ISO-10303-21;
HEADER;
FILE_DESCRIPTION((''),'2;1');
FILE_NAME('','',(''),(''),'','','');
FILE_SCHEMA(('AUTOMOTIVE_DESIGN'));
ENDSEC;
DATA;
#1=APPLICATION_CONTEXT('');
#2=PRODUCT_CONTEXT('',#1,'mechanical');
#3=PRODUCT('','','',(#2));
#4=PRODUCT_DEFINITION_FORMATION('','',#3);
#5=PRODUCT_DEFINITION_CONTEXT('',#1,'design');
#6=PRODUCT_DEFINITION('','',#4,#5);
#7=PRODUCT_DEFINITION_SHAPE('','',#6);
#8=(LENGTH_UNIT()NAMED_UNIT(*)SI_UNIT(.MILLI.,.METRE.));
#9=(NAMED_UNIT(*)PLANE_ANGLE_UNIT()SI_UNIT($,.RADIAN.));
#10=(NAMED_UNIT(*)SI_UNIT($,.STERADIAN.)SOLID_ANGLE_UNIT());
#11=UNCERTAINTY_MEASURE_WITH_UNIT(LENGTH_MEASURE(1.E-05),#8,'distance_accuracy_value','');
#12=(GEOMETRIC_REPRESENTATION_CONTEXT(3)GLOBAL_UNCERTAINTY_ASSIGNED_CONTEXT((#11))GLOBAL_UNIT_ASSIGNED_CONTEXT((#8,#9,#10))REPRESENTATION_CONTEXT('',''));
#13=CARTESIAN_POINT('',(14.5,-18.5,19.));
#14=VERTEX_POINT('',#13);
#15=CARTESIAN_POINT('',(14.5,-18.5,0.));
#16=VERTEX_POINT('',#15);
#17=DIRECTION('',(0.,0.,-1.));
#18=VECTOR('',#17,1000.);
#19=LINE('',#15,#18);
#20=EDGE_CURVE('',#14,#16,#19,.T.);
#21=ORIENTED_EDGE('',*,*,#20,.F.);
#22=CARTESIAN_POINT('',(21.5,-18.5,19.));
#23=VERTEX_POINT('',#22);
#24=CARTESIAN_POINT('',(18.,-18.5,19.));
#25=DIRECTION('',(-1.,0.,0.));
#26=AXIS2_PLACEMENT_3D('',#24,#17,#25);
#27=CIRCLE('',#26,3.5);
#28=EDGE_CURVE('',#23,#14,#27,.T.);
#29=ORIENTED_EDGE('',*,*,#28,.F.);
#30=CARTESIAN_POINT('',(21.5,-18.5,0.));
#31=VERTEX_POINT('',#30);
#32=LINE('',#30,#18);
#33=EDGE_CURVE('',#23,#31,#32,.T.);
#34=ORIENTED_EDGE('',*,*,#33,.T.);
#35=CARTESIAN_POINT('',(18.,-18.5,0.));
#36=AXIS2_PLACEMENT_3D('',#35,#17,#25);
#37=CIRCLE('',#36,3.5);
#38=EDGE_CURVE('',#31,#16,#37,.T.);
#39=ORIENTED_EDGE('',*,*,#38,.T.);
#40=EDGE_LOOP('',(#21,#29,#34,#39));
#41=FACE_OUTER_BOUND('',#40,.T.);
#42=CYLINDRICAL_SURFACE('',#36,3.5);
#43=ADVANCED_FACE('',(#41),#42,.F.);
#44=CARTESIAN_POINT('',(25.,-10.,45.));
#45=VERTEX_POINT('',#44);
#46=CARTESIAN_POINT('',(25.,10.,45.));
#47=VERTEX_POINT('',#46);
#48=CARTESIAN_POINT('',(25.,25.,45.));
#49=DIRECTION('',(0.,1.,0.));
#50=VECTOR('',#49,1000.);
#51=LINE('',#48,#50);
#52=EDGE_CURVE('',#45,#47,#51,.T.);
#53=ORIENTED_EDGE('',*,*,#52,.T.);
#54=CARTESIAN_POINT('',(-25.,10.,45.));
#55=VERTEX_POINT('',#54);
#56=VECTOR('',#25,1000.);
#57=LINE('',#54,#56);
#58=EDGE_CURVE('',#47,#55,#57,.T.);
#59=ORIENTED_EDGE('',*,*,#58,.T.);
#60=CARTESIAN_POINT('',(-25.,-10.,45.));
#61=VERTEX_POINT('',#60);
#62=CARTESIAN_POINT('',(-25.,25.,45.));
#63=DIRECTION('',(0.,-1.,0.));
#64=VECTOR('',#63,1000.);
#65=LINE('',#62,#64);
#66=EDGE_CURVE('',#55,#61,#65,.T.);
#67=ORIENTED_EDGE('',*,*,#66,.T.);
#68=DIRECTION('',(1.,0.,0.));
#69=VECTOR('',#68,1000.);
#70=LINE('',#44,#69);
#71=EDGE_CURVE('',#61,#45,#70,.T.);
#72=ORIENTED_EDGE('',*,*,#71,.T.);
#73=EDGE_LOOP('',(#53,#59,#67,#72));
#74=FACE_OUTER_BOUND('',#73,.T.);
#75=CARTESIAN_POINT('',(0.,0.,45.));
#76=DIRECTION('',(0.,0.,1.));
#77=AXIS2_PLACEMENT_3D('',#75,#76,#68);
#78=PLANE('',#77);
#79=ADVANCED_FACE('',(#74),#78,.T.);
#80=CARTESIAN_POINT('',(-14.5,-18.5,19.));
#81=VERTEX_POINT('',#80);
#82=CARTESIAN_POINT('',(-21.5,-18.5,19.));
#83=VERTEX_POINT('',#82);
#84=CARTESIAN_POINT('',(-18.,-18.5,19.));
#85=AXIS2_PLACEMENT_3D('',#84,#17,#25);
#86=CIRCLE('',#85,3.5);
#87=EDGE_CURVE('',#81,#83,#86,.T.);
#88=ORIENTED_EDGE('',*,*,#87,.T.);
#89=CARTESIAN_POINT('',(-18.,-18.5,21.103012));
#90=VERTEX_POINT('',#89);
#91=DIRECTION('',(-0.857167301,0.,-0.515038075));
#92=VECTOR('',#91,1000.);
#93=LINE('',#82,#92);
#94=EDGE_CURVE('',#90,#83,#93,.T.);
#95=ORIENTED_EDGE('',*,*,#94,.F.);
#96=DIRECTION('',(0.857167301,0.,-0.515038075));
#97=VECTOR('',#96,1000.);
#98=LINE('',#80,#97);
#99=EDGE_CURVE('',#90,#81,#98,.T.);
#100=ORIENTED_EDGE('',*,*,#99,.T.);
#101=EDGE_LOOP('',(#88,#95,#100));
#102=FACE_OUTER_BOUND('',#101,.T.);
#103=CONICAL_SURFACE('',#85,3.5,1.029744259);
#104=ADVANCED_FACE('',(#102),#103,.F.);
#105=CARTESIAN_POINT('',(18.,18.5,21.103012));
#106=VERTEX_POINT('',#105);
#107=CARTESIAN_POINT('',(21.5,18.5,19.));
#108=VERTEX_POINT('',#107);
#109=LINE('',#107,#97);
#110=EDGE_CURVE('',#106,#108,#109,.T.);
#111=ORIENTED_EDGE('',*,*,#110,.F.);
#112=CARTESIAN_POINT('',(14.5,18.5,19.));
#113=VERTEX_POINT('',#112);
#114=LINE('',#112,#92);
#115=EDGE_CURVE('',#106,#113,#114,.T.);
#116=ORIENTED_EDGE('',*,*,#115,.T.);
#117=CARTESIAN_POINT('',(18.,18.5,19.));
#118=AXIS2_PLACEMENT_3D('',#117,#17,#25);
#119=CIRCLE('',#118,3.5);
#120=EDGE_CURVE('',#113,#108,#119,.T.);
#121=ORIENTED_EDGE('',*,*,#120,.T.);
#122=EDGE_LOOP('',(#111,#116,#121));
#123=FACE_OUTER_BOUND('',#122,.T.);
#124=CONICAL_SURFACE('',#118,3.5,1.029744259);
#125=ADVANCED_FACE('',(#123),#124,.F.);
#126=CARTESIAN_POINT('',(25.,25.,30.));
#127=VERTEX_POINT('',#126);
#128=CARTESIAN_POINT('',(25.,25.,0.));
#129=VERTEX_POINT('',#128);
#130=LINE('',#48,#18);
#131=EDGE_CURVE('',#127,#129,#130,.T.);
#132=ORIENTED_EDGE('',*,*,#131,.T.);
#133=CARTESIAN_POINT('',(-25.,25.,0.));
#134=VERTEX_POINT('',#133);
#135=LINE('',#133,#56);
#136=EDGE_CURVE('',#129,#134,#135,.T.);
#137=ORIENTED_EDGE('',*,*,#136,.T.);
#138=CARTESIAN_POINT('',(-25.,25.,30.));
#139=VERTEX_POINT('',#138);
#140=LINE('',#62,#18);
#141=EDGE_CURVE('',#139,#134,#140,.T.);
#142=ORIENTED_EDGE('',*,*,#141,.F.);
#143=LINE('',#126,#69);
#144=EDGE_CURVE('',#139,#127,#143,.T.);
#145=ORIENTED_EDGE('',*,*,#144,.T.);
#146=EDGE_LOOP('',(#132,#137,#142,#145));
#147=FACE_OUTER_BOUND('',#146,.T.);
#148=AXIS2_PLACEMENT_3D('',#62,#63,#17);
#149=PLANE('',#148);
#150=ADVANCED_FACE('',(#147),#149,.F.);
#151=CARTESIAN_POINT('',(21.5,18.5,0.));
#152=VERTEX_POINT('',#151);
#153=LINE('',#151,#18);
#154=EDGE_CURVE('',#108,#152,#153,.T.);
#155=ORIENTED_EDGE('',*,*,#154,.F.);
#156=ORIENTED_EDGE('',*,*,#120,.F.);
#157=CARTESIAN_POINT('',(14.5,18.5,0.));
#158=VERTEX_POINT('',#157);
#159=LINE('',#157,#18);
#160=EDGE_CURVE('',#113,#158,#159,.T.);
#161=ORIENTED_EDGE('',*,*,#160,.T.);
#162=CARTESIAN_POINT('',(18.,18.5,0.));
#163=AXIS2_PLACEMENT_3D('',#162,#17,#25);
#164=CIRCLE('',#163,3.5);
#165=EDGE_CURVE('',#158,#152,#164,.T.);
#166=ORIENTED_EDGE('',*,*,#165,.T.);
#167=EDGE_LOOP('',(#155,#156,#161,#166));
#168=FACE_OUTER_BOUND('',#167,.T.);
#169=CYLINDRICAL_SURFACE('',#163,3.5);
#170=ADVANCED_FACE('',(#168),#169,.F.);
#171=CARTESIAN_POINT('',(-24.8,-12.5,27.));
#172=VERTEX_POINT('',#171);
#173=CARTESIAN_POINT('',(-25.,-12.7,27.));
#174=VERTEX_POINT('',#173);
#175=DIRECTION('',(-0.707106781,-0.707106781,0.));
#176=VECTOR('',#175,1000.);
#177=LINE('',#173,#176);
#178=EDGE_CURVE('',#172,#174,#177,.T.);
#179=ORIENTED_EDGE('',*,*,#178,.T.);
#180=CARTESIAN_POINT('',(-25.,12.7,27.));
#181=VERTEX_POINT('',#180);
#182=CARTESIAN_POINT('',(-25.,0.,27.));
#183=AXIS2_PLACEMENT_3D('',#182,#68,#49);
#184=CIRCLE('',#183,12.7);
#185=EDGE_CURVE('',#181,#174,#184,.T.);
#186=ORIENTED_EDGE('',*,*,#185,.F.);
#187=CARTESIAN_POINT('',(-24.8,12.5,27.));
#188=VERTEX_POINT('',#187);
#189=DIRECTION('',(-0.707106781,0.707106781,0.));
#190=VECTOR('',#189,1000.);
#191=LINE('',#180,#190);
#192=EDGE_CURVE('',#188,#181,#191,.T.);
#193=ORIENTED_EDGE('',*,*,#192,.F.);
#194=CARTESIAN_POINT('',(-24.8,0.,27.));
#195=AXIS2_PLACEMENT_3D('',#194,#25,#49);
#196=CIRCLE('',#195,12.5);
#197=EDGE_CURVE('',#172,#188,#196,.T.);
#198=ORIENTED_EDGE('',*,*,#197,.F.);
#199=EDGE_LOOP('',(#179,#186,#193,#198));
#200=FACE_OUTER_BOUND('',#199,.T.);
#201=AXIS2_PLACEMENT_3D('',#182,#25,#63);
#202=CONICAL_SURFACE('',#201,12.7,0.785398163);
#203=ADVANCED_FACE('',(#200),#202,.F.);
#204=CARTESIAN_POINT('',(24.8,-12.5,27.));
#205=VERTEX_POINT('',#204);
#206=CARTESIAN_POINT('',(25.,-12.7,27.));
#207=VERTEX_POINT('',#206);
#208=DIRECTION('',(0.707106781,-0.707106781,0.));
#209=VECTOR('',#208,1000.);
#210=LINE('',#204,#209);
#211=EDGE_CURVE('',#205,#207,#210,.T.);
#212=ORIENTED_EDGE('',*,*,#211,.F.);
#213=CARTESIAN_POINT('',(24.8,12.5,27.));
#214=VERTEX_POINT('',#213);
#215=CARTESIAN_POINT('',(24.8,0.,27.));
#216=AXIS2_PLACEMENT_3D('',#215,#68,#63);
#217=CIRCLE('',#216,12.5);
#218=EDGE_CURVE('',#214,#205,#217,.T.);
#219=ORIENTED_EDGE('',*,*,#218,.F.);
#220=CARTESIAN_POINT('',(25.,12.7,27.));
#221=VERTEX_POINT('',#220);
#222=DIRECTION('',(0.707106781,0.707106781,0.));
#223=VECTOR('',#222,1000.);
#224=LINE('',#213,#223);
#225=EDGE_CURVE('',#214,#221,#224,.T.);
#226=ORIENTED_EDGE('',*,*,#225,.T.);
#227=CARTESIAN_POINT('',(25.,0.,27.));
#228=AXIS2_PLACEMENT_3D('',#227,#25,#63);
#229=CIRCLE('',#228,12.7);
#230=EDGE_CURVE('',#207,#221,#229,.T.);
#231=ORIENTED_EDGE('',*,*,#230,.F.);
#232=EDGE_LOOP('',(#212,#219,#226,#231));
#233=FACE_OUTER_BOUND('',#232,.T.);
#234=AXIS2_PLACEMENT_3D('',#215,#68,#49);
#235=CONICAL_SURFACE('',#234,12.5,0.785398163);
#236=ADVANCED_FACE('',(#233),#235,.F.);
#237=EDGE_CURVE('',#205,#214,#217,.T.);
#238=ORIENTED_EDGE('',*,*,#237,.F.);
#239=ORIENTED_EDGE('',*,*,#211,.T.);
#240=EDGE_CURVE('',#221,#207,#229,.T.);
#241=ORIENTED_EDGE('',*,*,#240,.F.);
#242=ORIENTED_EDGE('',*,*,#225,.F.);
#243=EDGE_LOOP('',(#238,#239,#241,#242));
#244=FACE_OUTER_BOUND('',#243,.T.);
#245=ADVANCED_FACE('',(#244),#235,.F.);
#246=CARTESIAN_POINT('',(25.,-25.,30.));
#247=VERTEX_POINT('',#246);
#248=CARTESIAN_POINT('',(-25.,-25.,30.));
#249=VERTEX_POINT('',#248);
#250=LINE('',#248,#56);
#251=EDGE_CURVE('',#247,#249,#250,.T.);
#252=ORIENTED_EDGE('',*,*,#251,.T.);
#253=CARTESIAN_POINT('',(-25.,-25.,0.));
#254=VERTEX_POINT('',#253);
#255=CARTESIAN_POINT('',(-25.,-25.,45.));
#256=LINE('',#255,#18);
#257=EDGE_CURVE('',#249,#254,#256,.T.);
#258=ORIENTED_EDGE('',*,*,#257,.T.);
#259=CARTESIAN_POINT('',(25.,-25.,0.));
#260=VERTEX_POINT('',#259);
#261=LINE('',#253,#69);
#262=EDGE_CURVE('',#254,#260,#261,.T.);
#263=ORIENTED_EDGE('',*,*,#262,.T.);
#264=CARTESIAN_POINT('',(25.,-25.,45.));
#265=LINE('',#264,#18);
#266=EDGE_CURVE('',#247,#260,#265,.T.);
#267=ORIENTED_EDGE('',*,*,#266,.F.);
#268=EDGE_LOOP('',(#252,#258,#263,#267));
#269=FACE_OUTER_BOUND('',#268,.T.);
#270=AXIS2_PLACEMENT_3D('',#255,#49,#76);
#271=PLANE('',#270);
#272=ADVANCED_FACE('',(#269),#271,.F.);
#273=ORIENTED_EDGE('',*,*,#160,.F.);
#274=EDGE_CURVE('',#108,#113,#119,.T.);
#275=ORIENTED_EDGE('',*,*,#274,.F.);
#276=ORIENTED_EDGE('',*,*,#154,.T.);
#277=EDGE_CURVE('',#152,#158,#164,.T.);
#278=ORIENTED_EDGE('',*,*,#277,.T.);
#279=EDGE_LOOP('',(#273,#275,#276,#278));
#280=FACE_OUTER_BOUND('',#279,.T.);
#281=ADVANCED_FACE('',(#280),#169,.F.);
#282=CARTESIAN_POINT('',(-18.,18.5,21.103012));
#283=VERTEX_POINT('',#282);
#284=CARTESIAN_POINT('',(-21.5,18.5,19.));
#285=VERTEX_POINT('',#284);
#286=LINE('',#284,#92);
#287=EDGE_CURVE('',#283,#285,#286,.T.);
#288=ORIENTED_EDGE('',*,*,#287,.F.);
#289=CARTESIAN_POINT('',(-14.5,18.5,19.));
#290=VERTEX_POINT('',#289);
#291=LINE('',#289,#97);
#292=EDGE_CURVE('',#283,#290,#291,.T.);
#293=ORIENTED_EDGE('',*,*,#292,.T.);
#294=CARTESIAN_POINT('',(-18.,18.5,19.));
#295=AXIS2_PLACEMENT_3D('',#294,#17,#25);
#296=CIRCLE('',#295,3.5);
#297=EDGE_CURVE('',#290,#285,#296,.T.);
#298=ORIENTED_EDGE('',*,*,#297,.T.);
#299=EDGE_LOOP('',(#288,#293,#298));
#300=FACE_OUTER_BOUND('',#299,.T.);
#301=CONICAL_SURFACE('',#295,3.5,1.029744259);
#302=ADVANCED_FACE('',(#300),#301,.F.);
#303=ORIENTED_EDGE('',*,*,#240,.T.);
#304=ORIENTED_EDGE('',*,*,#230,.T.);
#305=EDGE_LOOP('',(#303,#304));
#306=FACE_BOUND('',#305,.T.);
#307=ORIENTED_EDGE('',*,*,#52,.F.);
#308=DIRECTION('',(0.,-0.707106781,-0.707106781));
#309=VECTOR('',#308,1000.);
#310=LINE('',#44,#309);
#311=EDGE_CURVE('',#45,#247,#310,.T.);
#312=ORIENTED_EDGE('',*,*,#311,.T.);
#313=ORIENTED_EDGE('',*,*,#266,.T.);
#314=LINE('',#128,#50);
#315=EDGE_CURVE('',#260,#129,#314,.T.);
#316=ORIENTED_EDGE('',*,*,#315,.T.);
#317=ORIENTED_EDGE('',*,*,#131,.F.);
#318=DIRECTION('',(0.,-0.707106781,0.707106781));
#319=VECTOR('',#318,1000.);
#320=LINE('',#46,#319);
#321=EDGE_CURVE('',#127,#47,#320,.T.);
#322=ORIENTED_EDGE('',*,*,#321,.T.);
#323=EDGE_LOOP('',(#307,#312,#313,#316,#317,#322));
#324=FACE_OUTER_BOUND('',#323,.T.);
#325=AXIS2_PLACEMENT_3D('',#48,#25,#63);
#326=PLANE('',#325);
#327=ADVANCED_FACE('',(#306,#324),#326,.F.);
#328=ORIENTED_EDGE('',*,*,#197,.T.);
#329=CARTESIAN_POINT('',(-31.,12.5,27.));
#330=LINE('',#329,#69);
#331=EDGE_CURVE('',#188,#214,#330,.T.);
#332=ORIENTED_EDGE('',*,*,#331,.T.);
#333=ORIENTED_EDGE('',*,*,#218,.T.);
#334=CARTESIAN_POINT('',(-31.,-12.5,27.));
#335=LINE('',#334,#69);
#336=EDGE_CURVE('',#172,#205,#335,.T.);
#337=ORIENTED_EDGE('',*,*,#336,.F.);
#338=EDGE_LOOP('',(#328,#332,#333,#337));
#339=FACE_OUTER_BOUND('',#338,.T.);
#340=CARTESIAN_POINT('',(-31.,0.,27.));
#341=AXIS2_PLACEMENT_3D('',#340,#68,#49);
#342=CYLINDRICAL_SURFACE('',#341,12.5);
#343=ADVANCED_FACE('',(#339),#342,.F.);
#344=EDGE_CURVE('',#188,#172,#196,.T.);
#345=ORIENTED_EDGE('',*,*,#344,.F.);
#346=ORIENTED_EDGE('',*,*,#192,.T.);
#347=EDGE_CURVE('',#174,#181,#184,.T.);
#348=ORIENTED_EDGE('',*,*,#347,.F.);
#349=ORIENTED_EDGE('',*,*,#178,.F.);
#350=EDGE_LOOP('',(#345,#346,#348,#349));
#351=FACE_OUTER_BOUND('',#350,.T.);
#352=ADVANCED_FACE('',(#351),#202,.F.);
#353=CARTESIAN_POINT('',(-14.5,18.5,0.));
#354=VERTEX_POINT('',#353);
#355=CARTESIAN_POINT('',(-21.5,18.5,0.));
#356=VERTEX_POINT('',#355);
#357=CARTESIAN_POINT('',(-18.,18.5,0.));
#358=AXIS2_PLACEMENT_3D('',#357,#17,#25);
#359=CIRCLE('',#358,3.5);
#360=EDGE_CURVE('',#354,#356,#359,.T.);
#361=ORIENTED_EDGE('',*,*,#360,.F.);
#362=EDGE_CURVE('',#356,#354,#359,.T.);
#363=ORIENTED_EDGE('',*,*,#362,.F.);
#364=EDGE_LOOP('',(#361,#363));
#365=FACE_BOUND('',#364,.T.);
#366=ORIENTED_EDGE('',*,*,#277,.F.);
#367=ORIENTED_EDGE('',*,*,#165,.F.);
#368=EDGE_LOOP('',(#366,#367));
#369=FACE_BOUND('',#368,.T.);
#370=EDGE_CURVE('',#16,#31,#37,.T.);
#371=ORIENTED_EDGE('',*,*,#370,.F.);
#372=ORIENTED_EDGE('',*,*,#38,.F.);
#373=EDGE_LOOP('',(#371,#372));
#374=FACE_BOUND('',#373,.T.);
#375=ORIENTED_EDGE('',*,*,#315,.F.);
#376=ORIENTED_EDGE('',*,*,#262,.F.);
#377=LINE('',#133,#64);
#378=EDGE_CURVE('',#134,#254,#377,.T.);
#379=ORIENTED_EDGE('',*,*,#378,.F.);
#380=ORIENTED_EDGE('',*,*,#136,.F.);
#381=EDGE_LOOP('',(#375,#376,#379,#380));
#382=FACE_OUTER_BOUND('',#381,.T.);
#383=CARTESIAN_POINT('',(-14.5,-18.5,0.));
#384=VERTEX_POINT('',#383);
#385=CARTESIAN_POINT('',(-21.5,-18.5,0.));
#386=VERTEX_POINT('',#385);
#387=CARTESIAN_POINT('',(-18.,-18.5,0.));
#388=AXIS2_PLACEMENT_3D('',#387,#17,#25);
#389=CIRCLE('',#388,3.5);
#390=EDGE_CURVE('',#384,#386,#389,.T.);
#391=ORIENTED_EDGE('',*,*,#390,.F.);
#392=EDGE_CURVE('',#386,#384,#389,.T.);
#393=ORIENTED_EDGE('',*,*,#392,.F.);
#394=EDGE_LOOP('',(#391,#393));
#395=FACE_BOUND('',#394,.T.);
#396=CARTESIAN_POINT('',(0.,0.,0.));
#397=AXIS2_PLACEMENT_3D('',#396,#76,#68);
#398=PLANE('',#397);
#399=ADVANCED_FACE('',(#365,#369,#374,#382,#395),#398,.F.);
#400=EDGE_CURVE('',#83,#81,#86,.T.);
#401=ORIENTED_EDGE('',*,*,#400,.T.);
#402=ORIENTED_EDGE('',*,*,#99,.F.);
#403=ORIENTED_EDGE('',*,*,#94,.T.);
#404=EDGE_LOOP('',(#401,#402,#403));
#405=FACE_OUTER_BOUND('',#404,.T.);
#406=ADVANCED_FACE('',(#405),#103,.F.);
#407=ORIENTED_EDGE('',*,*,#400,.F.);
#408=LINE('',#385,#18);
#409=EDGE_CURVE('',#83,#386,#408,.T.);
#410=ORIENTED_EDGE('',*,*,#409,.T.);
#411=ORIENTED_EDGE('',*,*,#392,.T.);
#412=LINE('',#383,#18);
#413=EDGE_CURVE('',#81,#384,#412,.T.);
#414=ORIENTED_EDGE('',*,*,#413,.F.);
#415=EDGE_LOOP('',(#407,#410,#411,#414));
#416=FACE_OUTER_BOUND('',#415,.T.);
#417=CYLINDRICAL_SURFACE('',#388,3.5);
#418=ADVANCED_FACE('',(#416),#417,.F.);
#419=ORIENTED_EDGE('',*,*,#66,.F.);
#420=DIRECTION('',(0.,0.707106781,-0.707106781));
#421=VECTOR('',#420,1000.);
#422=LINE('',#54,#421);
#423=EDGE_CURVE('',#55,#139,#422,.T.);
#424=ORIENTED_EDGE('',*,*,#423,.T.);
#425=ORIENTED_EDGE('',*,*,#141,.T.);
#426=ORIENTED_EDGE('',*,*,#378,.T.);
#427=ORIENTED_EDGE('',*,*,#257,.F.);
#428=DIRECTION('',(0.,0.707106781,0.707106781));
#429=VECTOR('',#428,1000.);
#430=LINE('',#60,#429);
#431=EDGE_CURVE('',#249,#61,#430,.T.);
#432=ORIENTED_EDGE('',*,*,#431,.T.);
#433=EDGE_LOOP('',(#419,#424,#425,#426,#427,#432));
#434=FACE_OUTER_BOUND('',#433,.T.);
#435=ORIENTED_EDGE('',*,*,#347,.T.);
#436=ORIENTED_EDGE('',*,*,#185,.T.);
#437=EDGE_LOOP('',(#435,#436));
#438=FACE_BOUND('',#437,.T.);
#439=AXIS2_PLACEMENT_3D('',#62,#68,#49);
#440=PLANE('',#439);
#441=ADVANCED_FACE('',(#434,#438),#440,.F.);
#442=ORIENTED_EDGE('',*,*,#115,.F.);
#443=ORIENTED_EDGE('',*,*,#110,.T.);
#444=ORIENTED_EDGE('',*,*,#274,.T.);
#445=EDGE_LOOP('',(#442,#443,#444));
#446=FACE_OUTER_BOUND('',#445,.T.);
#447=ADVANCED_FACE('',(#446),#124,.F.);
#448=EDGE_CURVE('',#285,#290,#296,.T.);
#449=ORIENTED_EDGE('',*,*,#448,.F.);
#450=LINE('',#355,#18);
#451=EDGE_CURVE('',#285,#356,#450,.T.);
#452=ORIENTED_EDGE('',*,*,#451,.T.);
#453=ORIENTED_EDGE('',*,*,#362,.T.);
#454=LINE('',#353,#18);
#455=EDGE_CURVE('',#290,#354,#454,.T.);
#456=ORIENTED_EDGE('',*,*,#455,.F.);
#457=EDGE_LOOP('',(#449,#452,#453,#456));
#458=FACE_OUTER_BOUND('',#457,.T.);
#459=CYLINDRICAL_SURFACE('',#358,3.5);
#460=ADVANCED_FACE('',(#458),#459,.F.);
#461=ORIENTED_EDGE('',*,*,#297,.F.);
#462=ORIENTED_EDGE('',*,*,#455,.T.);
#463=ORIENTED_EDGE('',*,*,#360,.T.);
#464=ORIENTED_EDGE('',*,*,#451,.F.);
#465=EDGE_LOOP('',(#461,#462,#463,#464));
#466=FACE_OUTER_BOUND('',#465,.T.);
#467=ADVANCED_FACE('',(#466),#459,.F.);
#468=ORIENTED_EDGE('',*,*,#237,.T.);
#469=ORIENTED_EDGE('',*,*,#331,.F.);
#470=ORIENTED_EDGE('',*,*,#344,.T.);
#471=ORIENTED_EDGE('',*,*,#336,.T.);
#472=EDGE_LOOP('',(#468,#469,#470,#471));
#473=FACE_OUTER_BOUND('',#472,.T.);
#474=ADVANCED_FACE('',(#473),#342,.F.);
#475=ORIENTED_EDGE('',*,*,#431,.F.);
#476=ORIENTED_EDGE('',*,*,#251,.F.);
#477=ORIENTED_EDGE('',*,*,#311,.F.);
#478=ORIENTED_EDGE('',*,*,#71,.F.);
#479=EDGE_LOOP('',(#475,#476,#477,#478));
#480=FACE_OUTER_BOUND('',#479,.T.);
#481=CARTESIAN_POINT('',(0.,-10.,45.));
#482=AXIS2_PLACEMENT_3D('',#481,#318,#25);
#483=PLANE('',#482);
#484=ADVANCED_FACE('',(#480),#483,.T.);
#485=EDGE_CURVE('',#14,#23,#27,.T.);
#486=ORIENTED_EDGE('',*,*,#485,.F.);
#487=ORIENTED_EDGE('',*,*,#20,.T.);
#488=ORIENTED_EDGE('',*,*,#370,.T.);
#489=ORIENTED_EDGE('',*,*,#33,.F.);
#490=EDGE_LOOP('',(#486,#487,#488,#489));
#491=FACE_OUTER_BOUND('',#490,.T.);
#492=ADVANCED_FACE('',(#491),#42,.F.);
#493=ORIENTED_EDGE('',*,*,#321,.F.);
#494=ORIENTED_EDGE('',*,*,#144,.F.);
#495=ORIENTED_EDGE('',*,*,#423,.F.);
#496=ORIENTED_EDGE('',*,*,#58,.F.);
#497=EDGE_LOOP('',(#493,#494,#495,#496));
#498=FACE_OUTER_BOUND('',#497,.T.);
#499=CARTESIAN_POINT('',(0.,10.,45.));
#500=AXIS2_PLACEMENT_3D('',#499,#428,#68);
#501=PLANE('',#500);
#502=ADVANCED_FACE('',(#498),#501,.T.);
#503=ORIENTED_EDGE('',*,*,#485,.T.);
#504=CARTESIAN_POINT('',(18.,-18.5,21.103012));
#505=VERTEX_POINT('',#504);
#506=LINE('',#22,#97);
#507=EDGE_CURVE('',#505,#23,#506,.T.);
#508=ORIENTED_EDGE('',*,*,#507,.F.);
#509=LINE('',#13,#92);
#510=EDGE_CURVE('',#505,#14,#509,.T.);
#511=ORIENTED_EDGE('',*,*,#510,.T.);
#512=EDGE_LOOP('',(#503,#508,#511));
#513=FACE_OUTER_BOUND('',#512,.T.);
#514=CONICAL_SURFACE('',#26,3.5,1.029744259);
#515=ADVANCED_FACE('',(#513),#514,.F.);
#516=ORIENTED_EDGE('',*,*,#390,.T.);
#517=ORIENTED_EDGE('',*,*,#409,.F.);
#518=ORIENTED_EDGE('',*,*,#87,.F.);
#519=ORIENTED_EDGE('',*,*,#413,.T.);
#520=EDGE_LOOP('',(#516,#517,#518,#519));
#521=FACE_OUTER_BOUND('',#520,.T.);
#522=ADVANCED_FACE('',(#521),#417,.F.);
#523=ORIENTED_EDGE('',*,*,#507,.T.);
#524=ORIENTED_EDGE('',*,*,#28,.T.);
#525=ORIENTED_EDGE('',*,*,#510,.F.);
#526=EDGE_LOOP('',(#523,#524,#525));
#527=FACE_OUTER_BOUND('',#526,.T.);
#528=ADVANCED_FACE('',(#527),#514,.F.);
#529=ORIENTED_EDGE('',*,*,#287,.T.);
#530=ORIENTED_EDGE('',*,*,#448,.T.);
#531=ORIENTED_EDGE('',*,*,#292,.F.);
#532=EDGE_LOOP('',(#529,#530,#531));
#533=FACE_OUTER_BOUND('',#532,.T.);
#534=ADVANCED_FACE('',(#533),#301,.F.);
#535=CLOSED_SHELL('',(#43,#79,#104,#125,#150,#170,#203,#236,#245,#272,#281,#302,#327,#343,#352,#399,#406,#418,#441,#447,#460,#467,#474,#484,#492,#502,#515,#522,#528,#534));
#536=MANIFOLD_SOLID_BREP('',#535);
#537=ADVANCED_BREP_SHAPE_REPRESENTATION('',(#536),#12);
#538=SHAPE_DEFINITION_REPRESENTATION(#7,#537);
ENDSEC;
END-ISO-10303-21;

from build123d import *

# Parameters (mm, degrees)
SKETCH1_W                 = 50
SKETCH1_H                 = 50
BOSS_EXTRUDE1_DEPTH       = 45
SKETCH3_R                 = 12.5
CUT_EXTRUDE1_DEPTH        = 56
CHAMFER1_SIZE             = 15
M8X1_0_TAPPED_HOLE1_D     = 7
M8X1_0_TAPPED_HOLE1_DEPTH = 19
M8X1_0_TAPPED_HOLE1_TIP   = 2.103012167
CHAMFER2_SIZE             = 0.2
CHAMFER3_SIZE             = 0.2


with BuildPart() as part:
    # Sketch1 → Boss-Extrude1 (new body)
    with BuildSketch(Plane.XY):
        Rectangle(SKETCH1_W, SKETCH1_H)
    extrude(amount=BOSS_EXTRUDE1_DEPTH)

    # Sketch3 → Cut-Extrude1 (cut)
    with BuildSketch(Plane(origin=(25, 0, 0), x_dir=(0, 0, -1), z_dir=(1, 0, 0))):
        with Locations(Location((-27, 0, 0), (0, 0, 90))):
            Circle(SKETCH3_R)
    extrude(amount=-CUT_EXTRUDE1_DEPTH, mode=Mode.SUBTRACT)

    # Chamfer1
    chamfer1_edges = [part.edges().sort_by_distance(p)[0] for p in [
        (0, -25, 45),
        (0, 25, 45),
    ]]
    chamfer(chamfer1_edges, length=CHAMFER1_SIZE)

    # M8x1.0 Tapped Hole1
    with Locations(Plane(origin=(0, 0, 0), x_dir=(-1, 0, 0), z_dir=(0, 0, -1))):
        with Locations((-18, 18.5), (18, 18.5), (18, -18.5), (-18, -18.5)):
            Hole(M8X1_0_TAPPED_HOLE1_D / 2, depth=M8X1_0_TAPPED_HOLE1_DEPTH)
            with Locations((0, 0, -(M8X1_0_TAPPED_HOLE1_DEPTH + M8X1_0_TAPPED_HOLE1_TIP / 2))):  # 118° drill point
                Cone(0, M8X1_0_TAPPED_HOLE1_D / 2, M8X1_0_TAPPED_HOLE1_TIP, mode=Mode.SUBTRACT)

    # Chamfer2
    chamfer2_edges = [part.edges().sort_by_distance(p)[0] for p in [
        (25, -12.5, 27),
    ]]
    chamfer(chamfer2_edges, length=CHAMFER2_SIZE)

    # Chamfer3
    chamfer3_edges = [part.edges().sort_by_distance(p)[0] for p in [
        (-25, -12.5, 27),
    ]]
    chamfer(chamfer3_edges, length=CHAMFER3_SIZE)


solid = part.part
